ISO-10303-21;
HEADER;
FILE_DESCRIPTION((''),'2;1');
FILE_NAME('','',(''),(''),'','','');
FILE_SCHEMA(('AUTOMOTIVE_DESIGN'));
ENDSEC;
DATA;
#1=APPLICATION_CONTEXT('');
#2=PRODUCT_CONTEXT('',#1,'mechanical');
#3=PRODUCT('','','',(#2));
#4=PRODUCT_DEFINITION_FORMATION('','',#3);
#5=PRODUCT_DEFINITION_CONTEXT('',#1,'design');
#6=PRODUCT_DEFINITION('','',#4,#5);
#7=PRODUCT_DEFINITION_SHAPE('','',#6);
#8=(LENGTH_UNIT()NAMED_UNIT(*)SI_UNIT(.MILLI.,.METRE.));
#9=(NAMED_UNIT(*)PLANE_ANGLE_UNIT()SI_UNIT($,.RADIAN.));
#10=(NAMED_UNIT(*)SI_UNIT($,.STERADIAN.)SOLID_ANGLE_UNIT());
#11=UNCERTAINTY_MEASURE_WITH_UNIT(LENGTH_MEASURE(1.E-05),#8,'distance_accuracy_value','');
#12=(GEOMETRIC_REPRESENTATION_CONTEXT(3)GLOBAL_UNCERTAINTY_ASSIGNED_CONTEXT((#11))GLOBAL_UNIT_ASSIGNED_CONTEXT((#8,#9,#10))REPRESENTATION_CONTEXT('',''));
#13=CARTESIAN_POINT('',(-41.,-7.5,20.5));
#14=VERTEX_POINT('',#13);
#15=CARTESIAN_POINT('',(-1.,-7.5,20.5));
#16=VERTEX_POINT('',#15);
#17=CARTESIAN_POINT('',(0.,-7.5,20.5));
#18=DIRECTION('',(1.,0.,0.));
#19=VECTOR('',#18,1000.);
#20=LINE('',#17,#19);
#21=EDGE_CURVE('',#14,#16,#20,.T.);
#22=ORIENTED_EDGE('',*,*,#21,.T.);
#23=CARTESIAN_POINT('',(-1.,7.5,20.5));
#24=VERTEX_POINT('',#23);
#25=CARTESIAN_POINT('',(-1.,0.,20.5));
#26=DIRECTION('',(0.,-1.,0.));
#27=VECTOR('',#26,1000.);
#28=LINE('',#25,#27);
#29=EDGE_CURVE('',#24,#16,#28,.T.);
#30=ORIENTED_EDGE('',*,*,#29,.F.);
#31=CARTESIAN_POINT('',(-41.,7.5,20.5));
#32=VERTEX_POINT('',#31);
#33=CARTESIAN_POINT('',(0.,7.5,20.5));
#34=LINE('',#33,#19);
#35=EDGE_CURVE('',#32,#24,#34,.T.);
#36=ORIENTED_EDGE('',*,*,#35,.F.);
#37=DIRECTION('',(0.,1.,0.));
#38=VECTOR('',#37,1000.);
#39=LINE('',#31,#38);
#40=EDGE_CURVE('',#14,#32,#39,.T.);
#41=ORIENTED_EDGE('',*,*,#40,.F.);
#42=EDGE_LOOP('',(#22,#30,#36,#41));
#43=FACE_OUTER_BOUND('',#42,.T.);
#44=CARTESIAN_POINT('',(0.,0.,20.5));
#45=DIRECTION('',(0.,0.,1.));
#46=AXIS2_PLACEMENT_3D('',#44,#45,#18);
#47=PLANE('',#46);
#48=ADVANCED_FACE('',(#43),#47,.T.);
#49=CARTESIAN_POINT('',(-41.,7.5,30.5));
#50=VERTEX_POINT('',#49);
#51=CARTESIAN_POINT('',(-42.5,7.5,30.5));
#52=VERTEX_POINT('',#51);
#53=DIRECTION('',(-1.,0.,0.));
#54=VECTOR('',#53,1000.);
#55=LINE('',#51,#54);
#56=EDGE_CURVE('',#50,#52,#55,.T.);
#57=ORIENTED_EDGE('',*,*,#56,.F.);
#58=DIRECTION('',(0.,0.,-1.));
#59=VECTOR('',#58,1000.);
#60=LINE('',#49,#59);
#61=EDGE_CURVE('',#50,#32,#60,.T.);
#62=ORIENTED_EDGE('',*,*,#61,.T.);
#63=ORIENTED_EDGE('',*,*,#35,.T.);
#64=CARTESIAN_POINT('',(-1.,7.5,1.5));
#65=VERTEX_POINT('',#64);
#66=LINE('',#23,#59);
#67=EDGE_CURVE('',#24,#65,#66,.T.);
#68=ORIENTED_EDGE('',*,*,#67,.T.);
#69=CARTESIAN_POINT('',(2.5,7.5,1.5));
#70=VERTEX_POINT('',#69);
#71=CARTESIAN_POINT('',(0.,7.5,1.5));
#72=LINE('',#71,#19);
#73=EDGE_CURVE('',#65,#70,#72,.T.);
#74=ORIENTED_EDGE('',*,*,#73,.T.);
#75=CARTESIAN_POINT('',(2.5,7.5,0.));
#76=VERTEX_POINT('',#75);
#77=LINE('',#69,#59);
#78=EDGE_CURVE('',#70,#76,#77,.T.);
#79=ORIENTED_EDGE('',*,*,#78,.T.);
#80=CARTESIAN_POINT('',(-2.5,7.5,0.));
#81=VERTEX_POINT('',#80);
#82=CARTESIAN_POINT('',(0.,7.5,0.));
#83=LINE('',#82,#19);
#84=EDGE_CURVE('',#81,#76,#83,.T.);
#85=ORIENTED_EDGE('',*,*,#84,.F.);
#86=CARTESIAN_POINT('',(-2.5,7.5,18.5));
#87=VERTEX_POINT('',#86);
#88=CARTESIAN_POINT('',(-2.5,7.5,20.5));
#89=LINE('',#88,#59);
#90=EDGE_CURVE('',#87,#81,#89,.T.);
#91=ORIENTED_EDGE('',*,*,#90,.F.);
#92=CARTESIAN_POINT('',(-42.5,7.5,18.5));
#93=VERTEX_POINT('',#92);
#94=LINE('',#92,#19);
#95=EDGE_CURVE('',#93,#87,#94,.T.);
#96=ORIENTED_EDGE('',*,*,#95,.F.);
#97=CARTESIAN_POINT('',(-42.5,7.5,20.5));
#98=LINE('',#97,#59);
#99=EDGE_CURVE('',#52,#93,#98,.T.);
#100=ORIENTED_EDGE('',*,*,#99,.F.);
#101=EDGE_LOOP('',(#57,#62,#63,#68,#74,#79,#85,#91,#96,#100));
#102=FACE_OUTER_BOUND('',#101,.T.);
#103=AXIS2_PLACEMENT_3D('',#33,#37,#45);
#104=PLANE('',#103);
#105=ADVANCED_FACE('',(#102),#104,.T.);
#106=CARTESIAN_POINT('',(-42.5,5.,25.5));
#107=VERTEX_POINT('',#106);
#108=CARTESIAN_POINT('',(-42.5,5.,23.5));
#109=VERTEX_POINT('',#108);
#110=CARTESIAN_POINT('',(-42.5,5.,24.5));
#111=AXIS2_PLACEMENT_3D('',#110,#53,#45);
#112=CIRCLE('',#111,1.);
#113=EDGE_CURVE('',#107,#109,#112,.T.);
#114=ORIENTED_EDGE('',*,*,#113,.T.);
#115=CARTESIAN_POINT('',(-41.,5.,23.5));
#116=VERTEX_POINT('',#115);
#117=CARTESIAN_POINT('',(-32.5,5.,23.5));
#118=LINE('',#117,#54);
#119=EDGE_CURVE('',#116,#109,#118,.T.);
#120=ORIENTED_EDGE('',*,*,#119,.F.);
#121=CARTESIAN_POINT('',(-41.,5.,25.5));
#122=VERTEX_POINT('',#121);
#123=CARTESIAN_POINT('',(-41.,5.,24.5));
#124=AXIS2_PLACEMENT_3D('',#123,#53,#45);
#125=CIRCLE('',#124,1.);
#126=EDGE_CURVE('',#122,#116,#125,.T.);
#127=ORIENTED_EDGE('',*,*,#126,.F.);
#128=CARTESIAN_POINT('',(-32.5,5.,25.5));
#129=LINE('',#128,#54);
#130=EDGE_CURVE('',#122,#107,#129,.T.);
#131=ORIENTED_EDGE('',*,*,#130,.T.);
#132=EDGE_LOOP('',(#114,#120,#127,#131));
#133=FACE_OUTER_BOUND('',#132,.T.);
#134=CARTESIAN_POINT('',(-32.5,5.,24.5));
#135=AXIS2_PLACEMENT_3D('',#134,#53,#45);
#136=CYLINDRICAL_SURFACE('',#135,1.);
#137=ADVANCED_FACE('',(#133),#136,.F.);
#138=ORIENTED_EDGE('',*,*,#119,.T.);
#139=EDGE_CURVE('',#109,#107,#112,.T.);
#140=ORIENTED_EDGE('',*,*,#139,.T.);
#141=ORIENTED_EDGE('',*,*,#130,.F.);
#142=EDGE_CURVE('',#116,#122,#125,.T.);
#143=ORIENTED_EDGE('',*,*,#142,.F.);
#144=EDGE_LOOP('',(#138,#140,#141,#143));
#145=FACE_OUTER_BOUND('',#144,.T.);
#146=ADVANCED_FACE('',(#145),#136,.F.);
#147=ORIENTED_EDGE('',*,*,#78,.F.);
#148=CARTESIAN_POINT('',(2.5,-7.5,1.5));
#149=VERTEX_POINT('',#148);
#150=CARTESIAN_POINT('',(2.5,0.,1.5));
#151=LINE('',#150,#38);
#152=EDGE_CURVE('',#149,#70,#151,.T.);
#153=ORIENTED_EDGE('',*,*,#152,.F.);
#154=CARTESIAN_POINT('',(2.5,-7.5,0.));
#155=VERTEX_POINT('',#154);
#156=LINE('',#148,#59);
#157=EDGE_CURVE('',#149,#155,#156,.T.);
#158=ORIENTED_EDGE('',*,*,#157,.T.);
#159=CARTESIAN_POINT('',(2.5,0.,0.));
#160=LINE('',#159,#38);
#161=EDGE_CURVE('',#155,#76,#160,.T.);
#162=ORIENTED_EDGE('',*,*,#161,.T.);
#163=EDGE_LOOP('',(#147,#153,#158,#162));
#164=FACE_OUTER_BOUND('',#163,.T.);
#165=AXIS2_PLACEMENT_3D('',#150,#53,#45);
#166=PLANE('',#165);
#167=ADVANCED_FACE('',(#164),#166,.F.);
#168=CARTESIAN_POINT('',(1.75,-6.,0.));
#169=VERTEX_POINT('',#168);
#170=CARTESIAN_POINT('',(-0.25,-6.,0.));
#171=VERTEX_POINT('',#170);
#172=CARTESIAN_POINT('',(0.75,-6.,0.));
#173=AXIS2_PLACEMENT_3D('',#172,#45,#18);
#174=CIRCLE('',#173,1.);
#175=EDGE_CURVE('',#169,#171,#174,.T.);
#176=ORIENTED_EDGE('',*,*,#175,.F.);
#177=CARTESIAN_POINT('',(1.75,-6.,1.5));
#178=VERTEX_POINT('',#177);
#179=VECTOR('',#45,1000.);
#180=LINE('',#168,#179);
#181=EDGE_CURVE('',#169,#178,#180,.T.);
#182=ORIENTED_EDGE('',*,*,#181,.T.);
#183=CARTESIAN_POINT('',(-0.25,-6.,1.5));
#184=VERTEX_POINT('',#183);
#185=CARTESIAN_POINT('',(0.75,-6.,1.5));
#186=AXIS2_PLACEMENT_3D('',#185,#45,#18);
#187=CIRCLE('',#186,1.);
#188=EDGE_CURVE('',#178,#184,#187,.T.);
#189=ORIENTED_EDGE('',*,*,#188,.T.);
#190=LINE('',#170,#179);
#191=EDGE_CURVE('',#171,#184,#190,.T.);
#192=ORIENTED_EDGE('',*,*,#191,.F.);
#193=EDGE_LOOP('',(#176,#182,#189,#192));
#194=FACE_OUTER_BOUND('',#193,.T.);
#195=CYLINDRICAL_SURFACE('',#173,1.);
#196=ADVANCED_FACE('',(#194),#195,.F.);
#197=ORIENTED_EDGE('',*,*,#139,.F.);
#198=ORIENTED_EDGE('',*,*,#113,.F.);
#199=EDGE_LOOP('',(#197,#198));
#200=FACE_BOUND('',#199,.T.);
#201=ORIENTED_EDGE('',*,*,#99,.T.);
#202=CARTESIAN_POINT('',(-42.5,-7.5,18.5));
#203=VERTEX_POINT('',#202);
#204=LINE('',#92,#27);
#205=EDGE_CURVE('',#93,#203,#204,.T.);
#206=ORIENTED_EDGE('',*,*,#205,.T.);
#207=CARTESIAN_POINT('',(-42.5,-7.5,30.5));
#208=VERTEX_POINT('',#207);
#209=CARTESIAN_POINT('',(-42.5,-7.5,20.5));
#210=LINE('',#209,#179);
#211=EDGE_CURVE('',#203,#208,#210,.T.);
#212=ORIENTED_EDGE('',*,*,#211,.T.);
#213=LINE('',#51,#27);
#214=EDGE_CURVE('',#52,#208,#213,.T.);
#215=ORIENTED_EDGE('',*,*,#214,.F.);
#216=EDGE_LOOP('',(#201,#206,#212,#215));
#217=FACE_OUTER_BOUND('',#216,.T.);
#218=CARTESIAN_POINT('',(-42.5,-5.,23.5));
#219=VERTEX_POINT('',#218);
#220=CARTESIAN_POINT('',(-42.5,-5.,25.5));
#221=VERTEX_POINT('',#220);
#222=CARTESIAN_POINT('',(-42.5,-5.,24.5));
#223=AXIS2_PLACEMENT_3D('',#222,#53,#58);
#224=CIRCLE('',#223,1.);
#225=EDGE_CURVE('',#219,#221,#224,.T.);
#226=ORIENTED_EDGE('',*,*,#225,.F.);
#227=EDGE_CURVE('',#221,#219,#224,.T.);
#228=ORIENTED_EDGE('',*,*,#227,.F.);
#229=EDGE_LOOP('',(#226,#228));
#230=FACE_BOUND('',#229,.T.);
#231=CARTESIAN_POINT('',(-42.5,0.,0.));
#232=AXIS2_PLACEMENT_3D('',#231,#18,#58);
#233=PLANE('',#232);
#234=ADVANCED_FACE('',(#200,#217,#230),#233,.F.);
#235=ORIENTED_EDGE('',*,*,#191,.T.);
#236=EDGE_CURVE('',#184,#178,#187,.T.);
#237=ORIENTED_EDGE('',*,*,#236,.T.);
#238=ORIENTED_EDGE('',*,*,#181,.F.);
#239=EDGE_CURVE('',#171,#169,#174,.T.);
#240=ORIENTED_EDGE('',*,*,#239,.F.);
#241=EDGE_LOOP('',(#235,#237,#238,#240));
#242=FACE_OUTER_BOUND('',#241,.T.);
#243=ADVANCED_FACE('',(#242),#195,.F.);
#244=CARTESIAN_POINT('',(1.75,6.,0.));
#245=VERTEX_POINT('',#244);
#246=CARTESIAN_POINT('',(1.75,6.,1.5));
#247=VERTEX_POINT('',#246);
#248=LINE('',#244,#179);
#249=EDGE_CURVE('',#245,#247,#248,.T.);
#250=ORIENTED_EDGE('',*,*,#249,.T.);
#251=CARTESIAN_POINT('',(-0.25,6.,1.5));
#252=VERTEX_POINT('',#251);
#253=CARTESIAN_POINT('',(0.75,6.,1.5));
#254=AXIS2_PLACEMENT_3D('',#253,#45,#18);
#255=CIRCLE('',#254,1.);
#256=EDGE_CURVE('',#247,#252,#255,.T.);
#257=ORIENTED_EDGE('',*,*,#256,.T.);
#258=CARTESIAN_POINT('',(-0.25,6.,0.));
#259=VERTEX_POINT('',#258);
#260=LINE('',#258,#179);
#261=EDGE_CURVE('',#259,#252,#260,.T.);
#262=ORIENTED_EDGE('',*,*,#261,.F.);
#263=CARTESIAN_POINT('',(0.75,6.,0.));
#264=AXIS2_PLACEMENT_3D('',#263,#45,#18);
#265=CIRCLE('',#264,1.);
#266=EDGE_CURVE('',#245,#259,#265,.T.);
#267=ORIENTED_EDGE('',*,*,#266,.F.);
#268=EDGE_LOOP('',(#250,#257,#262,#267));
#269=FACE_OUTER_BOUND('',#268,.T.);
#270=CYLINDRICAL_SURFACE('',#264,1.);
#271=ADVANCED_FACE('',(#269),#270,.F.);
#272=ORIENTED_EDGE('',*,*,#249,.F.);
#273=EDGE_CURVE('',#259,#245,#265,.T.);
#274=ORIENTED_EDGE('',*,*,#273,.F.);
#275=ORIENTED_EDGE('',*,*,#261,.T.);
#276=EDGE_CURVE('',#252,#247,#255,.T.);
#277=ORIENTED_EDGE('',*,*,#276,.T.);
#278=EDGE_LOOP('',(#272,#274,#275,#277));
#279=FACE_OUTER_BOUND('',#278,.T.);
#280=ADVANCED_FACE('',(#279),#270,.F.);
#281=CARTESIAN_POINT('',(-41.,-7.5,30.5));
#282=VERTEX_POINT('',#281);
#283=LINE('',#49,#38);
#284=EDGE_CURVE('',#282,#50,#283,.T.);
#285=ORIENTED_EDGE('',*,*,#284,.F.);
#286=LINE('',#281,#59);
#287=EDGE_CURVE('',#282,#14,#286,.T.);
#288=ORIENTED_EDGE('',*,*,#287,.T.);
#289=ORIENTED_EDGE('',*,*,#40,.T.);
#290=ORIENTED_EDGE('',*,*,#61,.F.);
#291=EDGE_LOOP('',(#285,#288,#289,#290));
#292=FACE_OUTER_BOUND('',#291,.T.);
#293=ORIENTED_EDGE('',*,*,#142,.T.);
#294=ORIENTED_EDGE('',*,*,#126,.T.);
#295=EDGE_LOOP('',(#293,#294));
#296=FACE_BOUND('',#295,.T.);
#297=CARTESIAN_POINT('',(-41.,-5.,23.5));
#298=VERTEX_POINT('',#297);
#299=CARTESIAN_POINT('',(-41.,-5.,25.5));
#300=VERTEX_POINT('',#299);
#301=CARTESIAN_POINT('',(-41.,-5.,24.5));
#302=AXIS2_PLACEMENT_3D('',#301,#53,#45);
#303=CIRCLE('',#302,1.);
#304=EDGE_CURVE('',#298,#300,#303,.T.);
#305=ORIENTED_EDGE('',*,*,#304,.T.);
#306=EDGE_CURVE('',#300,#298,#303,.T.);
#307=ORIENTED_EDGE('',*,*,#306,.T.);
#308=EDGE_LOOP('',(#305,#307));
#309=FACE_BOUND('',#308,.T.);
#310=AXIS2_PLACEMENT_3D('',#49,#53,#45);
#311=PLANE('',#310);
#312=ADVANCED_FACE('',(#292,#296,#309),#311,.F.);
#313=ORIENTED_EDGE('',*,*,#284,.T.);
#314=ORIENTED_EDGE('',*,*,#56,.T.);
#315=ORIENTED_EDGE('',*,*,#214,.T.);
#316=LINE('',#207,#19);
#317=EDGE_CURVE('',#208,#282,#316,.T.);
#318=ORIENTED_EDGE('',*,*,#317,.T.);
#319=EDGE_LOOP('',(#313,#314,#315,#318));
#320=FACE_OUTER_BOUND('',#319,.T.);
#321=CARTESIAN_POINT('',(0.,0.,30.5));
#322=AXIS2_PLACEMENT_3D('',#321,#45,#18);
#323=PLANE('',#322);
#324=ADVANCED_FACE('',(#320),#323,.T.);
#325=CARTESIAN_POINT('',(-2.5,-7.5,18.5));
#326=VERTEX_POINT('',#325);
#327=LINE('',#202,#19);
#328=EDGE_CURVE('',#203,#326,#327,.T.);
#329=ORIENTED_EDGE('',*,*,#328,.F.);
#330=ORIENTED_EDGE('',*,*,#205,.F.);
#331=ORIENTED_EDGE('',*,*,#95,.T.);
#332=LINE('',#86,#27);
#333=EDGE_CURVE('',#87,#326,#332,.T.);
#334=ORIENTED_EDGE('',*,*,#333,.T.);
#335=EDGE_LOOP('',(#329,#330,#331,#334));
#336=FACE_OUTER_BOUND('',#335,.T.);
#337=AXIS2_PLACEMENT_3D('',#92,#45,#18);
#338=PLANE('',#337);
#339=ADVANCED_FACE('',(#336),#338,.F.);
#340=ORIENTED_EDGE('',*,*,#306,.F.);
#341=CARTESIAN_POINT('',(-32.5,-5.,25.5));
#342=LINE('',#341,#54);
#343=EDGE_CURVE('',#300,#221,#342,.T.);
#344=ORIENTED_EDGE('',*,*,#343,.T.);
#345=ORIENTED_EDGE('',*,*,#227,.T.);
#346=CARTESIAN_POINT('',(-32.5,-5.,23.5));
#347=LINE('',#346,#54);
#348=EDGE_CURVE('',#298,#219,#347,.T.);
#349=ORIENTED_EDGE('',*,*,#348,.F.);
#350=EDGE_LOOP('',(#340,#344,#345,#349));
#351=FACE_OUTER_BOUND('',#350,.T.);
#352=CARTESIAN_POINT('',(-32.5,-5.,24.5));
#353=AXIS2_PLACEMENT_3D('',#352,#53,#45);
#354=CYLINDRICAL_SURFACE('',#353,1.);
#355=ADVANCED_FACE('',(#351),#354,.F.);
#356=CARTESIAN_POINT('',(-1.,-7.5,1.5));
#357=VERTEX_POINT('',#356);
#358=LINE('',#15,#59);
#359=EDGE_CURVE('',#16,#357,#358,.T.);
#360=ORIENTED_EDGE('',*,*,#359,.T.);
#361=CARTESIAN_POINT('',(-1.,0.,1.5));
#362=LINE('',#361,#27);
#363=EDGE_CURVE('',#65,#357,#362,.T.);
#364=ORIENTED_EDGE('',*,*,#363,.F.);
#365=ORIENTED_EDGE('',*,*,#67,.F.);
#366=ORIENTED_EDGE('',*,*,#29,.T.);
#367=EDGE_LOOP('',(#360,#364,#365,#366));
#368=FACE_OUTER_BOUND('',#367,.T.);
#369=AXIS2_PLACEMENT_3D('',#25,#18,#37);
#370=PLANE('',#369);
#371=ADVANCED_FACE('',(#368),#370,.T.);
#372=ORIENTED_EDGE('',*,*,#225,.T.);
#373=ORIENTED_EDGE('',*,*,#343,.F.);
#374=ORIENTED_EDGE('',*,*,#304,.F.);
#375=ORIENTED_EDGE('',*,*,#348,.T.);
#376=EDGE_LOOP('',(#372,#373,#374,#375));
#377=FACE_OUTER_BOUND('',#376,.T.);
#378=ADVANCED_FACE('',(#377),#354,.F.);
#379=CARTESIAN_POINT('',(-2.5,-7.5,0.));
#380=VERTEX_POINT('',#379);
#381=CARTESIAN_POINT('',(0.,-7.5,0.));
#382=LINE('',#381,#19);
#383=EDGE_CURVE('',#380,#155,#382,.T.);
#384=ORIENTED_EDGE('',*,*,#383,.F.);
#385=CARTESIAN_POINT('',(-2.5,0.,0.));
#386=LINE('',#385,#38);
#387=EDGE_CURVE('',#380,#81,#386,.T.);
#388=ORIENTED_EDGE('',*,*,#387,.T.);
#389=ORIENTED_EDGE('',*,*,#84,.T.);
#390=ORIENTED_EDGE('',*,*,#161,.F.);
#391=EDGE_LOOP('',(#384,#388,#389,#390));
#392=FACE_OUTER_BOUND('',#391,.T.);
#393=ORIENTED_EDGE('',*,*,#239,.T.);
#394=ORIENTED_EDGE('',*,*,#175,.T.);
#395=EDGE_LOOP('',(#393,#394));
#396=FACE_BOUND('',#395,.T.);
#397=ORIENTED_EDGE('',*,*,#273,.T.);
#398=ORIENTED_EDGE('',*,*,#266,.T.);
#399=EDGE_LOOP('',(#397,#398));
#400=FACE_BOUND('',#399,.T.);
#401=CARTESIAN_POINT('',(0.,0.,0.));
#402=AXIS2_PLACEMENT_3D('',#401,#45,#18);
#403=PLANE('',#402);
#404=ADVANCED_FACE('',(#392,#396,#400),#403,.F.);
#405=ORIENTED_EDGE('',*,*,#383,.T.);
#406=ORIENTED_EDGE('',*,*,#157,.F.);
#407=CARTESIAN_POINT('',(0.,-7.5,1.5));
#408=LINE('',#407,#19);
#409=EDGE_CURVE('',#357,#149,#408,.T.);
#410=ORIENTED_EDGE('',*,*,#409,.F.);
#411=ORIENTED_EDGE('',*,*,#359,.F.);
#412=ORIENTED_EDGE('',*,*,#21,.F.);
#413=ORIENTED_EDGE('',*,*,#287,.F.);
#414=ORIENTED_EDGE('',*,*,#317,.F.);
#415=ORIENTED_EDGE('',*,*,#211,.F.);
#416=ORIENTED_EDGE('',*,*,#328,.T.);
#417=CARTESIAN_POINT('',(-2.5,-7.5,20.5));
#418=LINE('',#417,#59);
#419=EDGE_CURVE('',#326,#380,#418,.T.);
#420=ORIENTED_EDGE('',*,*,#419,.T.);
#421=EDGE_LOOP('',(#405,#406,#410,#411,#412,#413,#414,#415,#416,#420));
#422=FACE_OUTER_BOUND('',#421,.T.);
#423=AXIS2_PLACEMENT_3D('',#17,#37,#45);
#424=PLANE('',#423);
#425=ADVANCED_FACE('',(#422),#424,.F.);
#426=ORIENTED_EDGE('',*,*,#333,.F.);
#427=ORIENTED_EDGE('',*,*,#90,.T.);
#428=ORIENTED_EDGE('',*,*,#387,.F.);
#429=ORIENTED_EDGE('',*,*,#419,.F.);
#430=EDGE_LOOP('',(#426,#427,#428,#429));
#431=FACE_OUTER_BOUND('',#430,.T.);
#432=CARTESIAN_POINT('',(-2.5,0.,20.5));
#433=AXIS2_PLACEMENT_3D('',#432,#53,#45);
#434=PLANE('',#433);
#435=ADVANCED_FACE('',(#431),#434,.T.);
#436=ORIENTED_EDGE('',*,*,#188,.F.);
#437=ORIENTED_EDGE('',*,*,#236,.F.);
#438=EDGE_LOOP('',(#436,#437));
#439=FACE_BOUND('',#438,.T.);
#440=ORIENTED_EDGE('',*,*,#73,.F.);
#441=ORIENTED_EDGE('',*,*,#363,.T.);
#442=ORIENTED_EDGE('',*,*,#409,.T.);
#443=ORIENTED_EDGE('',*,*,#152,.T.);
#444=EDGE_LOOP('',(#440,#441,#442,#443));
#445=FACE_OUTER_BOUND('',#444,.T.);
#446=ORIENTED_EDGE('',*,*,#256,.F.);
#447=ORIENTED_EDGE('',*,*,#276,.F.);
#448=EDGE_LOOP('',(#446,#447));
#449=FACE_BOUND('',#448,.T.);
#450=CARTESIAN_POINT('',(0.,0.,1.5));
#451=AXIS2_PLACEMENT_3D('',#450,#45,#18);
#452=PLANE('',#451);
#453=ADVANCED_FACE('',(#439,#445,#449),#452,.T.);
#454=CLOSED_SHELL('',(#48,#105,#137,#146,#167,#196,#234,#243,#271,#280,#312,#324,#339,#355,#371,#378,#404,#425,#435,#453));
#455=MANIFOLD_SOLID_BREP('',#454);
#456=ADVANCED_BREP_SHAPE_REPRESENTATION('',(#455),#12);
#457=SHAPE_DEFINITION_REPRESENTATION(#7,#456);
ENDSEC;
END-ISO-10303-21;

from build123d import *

# Parameters (mm, degrees)
SKETCH_1_W          = 1.5
SKETCH_1_H          = 15
EXTRUDE_1_DEPTH     = 20.5
SKETCH_1_5_W        = 3.5
SKETCH_1_5_H        = 15
EXTRUDE_2_DEPTH     = 1.5
SKETCH_2_R          = 1
CUT_EXTRUDE_1_DEPTH = 1.5
SKETCH_3_W          = 2
SKETCH_3_H          = 15
EXTRUDE_3_DEPTH     = 40
SKETCH_4_W          = 1.5
SKETCH_4_H          = 15
EXTRUDE_4_DEPTH     = 10
SKETCH_5_R          = 1
CUT_EXTRUDE_3_DEPTH = 10


with BuildPart() as part:
    # 草图1 → 凸台-拉伸1 (new body)
    with BuildSketch(Plane.XY):
        with Locations((-1.75, 0)):
            Rectangle(SKETCH_1_W, SKETCH_1_H)
    extrude(amount=EXTRUDE_1_DEPTH)

    # 草图1<5> → 凸台-拉伸2 (add)
    with BuildSketch(Plane.XY):
        with Locations((0.75, 0)):
            Rectangle(SKETCH_1_5_W, SKETCH_1_5_H)
    extrude(amount=EXTRUDE_2_DEPTH)

    # 草图2 → 切除-拉伸1 (cut)
    with BuildSketch(Plane.XY.offset(1.5)):
        with Locations((0.75, 6)):
            Circle(SKETCH_2_R)
        with Locations((0.75, -6)):
            Circle(SKETCH_2_R)
    extrude(amount=-CUT_EXTRUDE_1_DEPTH, mode=Mode.SUBTRACT)

    # 草图3 → 凸台-拉伸3 (add)
    with BuildSketch(Plane.ZY.offset(2.5)):
        with Locations((19.5, 0)):
            Rectangle(SKETCH_3_W, SKETCH_3_H)
    extrude(amount=EXTRUDE_3_DEPTH)

    # 草图4 → 凸台-拉伸4 (add)
    with BuildSketch(Plane.XY.offset(20.5)):
        with Locations((-41.75, 0)):
            Rectangle(SKETCH_4_W, SKETCH_4_H)
    extrude(amount=EXTRUDE_4_DEPTH)

    # 草图5 → 切除-拉伸3 (cut)
    with BuildSketch(Plane.ZY.offset(42.5)):
        with Locations((24.5, 5)):
            Circle(SKETCH_5_R)
        with Locations((24.5, -5)):
            Circle(SKETCH_5_R)
    extrude(amount=-CUT_EXTRUDE_3_DEPTH, mode=Mode.SUBTRACT)


solid = part.part
